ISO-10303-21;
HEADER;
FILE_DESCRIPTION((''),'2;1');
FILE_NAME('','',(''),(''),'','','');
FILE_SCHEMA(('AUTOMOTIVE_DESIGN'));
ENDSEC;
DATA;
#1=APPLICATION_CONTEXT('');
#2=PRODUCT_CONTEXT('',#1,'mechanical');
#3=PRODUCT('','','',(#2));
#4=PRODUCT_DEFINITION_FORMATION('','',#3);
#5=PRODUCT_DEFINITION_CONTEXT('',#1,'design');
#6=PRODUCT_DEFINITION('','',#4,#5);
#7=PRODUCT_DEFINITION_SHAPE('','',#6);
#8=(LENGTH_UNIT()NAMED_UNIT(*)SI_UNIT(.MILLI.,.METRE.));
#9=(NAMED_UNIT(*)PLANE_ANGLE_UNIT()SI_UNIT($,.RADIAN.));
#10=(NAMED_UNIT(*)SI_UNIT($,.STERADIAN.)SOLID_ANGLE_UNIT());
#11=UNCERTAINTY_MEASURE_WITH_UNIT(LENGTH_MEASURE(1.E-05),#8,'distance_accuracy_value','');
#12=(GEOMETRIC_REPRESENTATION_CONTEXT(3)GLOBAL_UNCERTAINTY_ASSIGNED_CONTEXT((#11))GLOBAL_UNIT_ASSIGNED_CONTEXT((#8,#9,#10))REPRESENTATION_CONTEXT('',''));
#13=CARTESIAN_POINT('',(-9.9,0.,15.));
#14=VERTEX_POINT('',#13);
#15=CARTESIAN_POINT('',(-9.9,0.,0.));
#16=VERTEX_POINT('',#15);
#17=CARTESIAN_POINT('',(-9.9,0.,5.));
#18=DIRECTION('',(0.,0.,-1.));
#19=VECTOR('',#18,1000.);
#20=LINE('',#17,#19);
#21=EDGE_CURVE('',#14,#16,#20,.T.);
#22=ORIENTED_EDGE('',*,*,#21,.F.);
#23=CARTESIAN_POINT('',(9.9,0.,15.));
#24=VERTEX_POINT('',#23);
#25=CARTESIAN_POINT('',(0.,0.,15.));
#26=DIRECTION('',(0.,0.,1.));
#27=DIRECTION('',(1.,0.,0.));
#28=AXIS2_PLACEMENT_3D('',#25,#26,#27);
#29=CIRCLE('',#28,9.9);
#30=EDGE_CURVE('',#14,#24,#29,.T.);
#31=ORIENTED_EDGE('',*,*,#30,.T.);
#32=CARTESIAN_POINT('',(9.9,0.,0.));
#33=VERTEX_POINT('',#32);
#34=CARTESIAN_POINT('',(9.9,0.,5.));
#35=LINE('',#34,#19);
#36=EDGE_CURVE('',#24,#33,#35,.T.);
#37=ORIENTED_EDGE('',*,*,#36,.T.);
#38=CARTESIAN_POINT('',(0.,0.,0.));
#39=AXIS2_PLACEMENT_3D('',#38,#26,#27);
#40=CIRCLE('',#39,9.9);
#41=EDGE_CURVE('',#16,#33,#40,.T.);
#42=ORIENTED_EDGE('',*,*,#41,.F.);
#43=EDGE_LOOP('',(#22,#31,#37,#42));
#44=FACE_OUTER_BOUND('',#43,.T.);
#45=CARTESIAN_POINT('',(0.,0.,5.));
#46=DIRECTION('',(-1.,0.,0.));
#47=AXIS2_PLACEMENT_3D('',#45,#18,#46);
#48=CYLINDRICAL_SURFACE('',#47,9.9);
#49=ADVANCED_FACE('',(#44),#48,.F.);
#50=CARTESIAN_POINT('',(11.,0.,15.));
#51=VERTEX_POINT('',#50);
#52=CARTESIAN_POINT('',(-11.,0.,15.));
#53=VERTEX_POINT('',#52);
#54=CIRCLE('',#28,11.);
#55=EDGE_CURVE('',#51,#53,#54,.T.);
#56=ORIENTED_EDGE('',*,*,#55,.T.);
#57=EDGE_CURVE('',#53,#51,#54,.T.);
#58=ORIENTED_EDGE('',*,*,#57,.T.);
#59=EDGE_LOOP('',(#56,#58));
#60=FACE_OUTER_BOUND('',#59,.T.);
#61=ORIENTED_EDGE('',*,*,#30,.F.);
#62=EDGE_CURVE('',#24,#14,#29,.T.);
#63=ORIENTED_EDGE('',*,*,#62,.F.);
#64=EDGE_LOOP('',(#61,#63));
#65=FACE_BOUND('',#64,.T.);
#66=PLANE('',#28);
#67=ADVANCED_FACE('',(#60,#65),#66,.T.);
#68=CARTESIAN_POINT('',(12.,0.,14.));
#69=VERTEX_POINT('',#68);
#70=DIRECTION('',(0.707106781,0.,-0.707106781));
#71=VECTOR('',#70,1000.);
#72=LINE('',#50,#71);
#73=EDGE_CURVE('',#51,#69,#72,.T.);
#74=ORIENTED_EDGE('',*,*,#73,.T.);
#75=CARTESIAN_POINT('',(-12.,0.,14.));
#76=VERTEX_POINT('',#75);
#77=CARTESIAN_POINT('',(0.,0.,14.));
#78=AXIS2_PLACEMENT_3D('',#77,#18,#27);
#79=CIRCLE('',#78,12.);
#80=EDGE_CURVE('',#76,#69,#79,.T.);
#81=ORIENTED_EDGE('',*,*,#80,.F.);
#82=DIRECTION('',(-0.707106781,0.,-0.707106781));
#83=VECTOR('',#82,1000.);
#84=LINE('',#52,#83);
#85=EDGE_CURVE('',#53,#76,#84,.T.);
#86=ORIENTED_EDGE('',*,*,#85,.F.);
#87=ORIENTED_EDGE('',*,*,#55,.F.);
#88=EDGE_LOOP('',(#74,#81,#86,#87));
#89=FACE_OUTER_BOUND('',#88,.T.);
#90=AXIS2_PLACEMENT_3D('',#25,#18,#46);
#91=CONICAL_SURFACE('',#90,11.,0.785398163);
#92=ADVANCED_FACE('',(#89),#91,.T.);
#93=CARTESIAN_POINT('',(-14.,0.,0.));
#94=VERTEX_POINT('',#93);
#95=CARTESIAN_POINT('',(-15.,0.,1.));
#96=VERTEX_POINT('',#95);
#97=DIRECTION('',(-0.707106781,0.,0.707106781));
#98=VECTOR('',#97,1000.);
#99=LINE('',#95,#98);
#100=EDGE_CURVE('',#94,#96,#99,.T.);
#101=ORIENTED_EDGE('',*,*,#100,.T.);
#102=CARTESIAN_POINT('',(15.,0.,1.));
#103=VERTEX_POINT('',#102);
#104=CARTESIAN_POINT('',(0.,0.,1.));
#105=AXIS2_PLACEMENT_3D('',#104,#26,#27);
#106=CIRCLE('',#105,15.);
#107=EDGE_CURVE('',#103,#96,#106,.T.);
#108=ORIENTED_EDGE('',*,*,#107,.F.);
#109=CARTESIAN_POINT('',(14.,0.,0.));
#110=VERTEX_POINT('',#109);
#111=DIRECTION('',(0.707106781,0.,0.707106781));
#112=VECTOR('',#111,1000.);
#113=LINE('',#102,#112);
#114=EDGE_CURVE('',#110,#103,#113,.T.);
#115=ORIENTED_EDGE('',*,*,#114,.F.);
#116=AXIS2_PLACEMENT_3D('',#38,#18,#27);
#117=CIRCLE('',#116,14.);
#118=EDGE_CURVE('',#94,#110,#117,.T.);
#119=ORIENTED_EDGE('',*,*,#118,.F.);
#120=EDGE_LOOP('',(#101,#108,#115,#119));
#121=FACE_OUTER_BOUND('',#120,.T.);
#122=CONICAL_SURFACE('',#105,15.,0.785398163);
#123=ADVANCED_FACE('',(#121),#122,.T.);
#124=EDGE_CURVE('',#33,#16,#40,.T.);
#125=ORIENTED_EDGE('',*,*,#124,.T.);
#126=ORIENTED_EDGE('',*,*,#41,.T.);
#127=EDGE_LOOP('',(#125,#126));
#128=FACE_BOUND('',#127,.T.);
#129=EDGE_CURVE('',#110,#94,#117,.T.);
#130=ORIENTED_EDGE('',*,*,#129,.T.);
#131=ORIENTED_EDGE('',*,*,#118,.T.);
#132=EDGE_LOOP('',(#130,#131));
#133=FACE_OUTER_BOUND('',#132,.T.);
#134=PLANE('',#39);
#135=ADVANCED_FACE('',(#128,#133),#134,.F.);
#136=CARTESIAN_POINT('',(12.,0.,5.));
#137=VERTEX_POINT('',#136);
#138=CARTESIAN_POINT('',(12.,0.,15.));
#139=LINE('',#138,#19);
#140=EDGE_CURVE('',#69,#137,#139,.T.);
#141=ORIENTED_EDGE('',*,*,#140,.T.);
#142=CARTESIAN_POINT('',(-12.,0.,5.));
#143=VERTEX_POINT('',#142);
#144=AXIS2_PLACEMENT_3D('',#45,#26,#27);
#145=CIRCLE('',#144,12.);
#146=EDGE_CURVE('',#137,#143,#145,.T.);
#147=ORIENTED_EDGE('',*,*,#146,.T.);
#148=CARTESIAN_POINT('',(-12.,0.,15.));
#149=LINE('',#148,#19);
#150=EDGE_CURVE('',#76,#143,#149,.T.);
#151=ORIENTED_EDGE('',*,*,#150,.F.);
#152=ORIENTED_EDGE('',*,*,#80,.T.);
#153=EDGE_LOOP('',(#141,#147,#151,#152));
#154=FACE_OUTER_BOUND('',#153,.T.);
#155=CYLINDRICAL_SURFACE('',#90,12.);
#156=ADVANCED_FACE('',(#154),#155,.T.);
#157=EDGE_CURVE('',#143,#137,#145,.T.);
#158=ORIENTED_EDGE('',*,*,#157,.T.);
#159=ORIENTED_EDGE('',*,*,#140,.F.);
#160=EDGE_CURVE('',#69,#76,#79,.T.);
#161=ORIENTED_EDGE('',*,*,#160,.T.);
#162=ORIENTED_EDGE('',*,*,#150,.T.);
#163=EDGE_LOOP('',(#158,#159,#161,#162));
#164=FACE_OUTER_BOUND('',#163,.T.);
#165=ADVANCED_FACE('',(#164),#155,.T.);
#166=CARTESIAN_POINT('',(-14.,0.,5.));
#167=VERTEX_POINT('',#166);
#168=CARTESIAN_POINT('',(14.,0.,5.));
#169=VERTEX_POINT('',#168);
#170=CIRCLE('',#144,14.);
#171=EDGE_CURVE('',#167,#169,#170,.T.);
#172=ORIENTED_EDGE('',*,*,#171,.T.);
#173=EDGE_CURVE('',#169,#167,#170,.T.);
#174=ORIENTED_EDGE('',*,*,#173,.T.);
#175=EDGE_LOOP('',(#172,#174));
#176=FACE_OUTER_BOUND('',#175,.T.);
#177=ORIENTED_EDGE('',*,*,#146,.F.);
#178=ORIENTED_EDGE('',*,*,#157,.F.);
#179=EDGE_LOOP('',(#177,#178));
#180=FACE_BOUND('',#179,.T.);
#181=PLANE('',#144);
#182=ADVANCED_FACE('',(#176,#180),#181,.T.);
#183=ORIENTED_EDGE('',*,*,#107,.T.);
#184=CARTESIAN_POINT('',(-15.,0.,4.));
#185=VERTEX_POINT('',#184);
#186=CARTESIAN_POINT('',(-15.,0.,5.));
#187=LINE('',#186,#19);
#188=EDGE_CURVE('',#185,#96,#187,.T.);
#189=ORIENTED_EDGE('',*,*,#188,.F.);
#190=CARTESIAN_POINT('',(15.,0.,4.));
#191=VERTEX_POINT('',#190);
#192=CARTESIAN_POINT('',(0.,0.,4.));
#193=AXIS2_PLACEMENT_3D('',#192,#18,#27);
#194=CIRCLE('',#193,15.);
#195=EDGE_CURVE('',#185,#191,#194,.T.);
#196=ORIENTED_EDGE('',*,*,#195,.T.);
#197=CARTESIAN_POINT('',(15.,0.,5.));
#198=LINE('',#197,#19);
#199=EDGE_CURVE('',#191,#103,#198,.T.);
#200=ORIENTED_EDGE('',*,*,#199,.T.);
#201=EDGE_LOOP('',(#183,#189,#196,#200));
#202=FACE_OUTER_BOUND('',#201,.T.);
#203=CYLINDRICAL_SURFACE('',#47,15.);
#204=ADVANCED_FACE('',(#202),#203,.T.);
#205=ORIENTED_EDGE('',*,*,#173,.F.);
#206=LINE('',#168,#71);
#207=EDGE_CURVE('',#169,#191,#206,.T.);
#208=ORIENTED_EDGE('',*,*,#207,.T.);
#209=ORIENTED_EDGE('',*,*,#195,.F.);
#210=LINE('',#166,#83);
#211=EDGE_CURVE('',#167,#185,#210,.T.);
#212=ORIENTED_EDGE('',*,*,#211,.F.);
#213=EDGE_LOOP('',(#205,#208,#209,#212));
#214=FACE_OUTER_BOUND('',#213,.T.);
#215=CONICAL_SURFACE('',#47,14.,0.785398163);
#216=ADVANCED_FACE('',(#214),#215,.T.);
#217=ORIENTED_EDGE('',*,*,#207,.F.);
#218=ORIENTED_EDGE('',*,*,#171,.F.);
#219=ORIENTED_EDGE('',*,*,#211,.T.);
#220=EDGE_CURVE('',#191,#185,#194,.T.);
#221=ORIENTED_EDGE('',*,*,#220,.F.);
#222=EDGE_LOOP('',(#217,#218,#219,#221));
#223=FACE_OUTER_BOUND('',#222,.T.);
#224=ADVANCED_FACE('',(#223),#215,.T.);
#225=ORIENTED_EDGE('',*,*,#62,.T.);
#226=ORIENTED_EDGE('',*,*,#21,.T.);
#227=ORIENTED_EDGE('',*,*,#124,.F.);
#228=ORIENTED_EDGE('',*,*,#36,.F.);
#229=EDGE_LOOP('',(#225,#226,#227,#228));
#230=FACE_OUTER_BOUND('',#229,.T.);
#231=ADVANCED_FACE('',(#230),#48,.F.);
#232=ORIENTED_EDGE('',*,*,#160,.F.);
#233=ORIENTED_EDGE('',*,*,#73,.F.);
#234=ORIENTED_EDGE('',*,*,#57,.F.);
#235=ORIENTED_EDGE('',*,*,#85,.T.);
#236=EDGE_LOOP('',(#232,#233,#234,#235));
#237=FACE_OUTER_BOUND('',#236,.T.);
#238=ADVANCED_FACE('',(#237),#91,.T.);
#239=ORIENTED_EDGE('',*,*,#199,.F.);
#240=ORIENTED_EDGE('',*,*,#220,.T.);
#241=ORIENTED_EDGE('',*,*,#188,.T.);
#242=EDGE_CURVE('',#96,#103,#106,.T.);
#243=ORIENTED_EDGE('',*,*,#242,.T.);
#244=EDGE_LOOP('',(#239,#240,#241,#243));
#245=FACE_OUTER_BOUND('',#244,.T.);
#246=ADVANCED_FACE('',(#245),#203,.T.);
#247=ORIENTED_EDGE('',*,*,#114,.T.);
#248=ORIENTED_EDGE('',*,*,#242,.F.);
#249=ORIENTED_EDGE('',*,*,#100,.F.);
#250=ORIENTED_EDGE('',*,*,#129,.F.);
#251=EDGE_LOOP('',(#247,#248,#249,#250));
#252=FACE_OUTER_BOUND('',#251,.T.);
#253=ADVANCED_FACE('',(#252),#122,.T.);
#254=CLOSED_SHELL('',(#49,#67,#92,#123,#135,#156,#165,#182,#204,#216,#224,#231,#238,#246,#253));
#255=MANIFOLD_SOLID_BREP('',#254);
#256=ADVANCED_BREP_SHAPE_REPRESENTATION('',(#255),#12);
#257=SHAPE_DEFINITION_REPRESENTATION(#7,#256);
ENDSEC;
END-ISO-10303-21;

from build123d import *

# Parameters (mm, degrees)
SKETCH2_R           = 15
SKETCH2_R_2         = 9.9
BOSS_EXTRUDE1_DEPTH = 5
SKETCH3_R           = 12
SKETCH3_R_2         = 9.9
BOSS_EXTRUDE2_DEPTH = 10
CHAMFER1_SIZE       = 1


with BuildPart() as part:
    # Sketch2 → Boss-Extrude1 (new body)
    with BuildSketch(Plane.XY):
        Circle(SKETCH2_R)
        Circle(SKETCH2_R_2, mode=Mode.SUBTRACT)
    extrude(amount=BOSS_EXTRUDE1_DEPTH)

    # Sketch3 → Boss-Extrude2 (add)
    with BuildSketch(Plane.XY.offset(5)):
        Circle(SKETCH3_R)
        Circle(SKETCH3_R_2, mode=Mode.SUBTRACT)
    extrude(amount=BOSS_EXTRUDE2_DEPTH)

    # Chamfer1
    chamfer1_edges = [part.edges().sort_by_distance(p)[0] for p in [
        (-12, 0, 15),
        (-15, 0, 0),
        (-15, 0, 5),
    ]]
    chamfer(chamfer1_edges, length=CHAMFER1_SIZE)


solid = part.part
